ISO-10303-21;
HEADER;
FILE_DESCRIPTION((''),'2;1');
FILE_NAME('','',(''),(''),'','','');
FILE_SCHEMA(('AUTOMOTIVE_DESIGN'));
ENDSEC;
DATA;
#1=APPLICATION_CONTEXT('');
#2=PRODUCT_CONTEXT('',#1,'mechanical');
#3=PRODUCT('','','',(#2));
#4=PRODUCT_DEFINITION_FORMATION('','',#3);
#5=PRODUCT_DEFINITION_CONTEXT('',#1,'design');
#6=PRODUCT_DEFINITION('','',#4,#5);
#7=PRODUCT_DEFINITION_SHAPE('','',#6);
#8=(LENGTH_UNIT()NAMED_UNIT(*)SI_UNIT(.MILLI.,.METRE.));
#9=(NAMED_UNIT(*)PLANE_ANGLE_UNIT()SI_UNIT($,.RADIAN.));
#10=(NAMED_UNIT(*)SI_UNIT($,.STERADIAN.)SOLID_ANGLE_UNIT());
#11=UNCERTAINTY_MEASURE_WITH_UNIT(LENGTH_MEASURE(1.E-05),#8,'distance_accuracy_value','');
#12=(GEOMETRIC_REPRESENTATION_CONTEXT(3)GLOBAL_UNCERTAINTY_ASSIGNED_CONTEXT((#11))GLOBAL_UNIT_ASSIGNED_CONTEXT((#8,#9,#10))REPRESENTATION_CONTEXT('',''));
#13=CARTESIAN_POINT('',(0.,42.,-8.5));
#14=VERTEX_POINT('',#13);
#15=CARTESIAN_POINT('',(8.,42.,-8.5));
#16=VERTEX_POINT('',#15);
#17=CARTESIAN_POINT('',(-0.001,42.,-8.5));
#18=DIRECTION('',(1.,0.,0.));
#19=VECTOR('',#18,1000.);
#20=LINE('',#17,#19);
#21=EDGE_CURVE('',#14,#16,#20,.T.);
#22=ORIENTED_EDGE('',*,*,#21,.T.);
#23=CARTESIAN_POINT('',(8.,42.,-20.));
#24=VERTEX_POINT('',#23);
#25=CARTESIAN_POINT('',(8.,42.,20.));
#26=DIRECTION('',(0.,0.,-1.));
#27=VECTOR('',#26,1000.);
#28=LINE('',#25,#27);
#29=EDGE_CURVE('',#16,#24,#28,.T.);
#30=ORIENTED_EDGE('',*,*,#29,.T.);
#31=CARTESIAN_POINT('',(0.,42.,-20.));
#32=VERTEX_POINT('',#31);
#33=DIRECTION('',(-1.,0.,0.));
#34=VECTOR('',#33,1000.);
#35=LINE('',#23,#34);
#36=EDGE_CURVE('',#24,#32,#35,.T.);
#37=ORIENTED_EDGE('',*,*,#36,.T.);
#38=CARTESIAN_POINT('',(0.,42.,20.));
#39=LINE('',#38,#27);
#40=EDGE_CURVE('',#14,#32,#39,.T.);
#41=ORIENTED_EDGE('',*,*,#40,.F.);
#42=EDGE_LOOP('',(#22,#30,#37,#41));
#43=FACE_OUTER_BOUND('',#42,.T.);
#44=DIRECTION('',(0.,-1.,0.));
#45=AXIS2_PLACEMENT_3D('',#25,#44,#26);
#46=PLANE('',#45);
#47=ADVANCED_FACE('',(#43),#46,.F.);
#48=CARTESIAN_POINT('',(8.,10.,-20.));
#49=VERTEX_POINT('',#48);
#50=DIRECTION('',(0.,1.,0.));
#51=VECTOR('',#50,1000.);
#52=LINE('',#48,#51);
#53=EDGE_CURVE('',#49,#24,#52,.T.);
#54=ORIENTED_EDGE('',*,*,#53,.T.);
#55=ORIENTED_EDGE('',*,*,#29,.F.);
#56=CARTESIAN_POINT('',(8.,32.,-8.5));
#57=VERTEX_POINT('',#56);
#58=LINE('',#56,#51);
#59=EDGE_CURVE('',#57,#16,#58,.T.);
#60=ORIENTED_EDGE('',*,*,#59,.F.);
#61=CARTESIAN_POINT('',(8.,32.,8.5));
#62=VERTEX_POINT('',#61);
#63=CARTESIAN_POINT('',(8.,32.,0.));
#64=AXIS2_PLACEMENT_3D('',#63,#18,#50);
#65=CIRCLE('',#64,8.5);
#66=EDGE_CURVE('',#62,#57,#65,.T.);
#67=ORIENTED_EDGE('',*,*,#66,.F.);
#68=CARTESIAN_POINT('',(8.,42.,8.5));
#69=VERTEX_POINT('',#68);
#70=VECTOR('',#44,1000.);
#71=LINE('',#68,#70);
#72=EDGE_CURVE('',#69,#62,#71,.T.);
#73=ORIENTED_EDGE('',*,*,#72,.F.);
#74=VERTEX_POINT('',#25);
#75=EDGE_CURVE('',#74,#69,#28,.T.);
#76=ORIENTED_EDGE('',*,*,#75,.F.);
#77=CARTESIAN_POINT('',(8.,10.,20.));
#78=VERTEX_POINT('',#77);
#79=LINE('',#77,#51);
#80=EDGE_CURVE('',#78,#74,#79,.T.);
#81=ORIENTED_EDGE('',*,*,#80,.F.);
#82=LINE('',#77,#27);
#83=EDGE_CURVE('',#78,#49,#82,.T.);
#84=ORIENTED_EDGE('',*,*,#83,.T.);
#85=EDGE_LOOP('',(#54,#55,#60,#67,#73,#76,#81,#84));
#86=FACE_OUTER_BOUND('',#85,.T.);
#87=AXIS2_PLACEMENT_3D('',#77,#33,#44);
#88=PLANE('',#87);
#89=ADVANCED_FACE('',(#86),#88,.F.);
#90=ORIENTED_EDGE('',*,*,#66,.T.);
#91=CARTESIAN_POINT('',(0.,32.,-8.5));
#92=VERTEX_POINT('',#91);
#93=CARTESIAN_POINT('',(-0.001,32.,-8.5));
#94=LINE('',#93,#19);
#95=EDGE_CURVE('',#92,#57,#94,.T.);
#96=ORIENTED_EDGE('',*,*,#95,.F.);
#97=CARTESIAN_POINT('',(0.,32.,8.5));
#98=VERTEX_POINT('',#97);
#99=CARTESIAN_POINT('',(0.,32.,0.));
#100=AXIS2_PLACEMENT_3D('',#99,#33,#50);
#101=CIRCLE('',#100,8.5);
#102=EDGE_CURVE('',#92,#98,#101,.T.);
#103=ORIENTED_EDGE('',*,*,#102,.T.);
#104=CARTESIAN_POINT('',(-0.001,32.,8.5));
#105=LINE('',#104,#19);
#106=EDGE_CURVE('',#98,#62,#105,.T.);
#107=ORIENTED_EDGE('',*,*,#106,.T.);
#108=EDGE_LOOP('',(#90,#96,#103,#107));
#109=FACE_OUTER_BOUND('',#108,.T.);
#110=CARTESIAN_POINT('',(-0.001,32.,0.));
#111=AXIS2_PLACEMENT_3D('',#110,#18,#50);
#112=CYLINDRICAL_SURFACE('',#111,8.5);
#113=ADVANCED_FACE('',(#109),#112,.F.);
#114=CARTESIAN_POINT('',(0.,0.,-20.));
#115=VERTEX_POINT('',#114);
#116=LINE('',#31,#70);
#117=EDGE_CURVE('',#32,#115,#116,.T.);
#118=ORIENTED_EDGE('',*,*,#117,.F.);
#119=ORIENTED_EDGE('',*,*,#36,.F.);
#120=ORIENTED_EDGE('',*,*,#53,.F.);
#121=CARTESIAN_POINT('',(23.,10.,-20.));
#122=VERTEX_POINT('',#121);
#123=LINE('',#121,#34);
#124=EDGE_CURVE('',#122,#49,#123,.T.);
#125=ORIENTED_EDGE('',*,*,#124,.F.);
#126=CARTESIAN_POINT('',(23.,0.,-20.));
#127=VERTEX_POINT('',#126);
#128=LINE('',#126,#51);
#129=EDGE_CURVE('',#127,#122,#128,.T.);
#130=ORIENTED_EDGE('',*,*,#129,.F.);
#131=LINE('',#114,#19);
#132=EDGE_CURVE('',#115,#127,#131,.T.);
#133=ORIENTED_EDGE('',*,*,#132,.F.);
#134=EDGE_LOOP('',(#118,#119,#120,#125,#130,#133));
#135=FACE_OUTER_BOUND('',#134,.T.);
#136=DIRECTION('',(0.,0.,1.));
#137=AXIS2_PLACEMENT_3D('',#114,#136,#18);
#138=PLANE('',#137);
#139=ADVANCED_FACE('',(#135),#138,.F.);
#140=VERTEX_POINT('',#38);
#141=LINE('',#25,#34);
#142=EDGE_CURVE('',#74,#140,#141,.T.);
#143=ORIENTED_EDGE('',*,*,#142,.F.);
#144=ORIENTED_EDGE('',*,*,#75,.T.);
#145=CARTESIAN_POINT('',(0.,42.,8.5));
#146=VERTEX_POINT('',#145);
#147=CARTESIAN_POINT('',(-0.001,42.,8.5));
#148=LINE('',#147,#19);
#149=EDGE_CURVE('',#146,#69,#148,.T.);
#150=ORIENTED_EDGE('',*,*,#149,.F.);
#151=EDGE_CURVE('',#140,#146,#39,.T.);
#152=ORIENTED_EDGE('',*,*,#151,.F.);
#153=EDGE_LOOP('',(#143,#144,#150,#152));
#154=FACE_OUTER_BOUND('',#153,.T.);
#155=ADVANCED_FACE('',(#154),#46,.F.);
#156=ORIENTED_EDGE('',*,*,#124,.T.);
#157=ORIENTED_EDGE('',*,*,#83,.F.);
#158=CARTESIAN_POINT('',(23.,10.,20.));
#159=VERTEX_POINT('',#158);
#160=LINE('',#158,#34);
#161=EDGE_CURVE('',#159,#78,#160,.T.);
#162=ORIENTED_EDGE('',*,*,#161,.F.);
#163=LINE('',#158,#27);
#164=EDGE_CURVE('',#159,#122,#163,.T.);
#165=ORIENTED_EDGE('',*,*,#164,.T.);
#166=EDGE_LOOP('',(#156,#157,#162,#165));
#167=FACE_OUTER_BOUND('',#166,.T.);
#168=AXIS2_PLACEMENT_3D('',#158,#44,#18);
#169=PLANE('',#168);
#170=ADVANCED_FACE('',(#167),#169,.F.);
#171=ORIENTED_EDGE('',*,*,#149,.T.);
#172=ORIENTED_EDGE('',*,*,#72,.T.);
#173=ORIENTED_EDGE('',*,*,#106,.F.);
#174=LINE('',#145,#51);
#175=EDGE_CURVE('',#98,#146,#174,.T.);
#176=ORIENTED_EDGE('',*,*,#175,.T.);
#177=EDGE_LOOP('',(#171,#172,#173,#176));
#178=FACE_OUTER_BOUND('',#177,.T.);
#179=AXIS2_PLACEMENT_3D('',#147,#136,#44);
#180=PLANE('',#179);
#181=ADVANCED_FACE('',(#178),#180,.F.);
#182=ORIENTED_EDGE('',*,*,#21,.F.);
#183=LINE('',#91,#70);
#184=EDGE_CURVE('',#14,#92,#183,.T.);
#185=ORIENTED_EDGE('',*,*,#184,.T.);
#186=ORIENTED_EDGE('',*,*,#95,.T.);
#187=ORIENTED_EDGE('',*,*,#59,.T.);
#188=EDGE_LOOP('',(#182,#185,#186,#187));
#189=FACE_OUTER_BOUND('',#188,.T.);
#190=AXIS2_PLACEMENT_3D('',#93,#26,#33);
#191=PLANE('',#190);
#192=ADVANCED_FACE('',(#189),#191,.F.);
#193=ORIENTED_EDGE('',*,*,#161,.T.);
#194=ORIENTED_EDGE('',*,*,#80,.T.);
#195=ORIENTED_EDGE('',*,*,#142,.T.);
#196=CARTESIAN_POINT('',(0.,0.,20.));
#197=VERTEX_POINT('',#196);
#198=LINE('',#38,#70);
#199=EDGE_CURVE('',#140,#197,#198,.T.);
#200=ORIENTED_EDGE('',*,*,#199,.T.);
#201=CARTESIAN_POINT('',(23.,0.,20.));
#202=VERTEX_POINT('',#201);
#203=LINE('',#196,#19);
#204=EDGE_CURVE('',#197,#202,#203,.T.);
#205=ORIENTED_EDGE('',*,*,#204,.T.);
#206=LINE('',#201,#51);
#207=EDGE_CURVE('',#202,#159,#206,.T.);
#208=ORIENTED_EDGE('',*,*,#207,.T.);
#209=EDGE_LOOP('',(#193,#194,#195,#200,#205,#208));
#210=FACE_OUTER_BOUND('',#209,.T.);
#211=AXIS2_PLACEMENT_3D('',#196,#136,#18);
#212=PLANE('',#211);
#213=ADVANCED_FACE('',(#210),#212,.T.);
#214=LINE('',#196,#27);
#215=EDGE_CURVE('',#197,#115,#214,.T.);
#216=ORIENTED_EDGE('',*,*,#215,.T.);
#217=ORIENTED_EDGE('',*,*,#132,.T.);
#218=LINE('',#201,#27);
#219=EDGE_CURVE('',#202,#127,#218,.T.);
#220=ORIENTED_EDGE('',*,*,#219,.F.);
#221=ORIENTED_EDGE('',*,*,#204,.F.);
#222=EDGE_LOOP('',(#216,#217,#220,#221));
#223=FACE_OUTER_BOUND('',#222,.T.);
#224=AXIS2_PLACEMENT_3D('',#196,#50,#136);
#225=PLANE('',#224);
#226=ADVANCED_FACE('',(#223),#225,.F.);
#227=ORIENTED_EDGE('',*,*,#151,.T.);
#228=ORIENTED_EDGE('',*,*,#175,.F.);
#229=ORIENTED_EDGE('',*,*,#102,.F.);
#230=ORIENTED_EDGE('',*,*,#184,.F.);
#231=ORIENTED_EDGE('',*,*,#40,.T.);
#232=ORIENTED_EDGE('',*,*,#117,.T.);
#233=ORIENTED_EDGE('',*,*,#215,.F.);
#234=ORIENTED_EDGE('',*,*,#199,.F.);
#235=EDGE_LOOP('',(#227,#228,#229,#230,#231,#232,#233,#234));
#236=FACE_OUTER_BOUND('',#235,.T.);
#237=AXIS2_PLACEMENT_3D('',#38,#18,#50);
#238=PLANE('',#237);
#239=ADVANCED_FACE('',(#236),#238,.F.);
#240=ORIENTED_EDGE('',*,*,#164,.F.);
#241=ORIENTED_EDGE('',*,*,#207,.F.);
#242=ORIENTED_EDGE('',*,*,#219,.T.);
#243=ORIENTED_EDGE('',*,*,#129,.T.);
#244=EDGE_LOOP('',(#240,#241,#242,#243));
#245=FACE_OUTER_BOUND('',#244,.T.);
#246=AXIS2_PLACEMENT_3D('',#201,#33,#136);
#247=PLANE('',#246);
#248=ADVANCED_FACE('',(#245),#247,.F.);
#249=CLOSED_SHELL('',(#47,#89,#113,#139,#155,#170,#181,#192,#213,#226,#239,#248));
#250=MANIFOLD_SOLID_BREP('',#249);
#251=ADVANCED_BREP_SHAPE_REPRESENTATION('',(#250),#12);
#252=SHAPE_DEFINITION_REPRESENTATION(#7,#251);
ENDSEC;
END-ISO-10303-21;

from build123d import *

# Parameters (mm, degrees)
EXTRUDE_1_DEPTH     = 20
CUT_EXTRUDE_1_REACH = 50.877


with BuildPart() as part:
    # 草图1 → 凸台-拉伸1 (new, symmetric)
    with BuildSketch(Plane.XY):
        Polygon((0, 0), (23, 0), (23, 10), (8, 10), (8, 42), (0, 42), align=None)
    extrude(amount=EXTRUDE_1_DEPTH, both=True)

    # 草图2 → 切除-拉伸1 (cut, up to next)
    with BuildSketch(Plane(origin=(8, 0, 0), x_dir=(0, 0, -1), z_dir=(1, 0, 0)), mode=Mode.PRIVATE) as cut_extrude_1_sk1:
        with BuildLine():
            Line((-8.5, 42), (-8.5, 32))
            ThreePointArc((-8.5, 32), (0, 23.5), (8.5, 32))
            Line((8.5, 32), (8.5, 42))
            Line((8.5, 42), (-8.5, 42))
        make_face()
    cut_extrude_1_tool1 = extrude(cut_extrude_1_sk1.sketch, amount=-CUT_EXTRUDE_1_REACH, mode=Mode.PRIVATE) & part.part
    add(cut_extrude_1_tool1.solids().sort_by_distance((8, 33.55414, 0))[0], mode=Mode.SUBTRACT)


solid = part.part
